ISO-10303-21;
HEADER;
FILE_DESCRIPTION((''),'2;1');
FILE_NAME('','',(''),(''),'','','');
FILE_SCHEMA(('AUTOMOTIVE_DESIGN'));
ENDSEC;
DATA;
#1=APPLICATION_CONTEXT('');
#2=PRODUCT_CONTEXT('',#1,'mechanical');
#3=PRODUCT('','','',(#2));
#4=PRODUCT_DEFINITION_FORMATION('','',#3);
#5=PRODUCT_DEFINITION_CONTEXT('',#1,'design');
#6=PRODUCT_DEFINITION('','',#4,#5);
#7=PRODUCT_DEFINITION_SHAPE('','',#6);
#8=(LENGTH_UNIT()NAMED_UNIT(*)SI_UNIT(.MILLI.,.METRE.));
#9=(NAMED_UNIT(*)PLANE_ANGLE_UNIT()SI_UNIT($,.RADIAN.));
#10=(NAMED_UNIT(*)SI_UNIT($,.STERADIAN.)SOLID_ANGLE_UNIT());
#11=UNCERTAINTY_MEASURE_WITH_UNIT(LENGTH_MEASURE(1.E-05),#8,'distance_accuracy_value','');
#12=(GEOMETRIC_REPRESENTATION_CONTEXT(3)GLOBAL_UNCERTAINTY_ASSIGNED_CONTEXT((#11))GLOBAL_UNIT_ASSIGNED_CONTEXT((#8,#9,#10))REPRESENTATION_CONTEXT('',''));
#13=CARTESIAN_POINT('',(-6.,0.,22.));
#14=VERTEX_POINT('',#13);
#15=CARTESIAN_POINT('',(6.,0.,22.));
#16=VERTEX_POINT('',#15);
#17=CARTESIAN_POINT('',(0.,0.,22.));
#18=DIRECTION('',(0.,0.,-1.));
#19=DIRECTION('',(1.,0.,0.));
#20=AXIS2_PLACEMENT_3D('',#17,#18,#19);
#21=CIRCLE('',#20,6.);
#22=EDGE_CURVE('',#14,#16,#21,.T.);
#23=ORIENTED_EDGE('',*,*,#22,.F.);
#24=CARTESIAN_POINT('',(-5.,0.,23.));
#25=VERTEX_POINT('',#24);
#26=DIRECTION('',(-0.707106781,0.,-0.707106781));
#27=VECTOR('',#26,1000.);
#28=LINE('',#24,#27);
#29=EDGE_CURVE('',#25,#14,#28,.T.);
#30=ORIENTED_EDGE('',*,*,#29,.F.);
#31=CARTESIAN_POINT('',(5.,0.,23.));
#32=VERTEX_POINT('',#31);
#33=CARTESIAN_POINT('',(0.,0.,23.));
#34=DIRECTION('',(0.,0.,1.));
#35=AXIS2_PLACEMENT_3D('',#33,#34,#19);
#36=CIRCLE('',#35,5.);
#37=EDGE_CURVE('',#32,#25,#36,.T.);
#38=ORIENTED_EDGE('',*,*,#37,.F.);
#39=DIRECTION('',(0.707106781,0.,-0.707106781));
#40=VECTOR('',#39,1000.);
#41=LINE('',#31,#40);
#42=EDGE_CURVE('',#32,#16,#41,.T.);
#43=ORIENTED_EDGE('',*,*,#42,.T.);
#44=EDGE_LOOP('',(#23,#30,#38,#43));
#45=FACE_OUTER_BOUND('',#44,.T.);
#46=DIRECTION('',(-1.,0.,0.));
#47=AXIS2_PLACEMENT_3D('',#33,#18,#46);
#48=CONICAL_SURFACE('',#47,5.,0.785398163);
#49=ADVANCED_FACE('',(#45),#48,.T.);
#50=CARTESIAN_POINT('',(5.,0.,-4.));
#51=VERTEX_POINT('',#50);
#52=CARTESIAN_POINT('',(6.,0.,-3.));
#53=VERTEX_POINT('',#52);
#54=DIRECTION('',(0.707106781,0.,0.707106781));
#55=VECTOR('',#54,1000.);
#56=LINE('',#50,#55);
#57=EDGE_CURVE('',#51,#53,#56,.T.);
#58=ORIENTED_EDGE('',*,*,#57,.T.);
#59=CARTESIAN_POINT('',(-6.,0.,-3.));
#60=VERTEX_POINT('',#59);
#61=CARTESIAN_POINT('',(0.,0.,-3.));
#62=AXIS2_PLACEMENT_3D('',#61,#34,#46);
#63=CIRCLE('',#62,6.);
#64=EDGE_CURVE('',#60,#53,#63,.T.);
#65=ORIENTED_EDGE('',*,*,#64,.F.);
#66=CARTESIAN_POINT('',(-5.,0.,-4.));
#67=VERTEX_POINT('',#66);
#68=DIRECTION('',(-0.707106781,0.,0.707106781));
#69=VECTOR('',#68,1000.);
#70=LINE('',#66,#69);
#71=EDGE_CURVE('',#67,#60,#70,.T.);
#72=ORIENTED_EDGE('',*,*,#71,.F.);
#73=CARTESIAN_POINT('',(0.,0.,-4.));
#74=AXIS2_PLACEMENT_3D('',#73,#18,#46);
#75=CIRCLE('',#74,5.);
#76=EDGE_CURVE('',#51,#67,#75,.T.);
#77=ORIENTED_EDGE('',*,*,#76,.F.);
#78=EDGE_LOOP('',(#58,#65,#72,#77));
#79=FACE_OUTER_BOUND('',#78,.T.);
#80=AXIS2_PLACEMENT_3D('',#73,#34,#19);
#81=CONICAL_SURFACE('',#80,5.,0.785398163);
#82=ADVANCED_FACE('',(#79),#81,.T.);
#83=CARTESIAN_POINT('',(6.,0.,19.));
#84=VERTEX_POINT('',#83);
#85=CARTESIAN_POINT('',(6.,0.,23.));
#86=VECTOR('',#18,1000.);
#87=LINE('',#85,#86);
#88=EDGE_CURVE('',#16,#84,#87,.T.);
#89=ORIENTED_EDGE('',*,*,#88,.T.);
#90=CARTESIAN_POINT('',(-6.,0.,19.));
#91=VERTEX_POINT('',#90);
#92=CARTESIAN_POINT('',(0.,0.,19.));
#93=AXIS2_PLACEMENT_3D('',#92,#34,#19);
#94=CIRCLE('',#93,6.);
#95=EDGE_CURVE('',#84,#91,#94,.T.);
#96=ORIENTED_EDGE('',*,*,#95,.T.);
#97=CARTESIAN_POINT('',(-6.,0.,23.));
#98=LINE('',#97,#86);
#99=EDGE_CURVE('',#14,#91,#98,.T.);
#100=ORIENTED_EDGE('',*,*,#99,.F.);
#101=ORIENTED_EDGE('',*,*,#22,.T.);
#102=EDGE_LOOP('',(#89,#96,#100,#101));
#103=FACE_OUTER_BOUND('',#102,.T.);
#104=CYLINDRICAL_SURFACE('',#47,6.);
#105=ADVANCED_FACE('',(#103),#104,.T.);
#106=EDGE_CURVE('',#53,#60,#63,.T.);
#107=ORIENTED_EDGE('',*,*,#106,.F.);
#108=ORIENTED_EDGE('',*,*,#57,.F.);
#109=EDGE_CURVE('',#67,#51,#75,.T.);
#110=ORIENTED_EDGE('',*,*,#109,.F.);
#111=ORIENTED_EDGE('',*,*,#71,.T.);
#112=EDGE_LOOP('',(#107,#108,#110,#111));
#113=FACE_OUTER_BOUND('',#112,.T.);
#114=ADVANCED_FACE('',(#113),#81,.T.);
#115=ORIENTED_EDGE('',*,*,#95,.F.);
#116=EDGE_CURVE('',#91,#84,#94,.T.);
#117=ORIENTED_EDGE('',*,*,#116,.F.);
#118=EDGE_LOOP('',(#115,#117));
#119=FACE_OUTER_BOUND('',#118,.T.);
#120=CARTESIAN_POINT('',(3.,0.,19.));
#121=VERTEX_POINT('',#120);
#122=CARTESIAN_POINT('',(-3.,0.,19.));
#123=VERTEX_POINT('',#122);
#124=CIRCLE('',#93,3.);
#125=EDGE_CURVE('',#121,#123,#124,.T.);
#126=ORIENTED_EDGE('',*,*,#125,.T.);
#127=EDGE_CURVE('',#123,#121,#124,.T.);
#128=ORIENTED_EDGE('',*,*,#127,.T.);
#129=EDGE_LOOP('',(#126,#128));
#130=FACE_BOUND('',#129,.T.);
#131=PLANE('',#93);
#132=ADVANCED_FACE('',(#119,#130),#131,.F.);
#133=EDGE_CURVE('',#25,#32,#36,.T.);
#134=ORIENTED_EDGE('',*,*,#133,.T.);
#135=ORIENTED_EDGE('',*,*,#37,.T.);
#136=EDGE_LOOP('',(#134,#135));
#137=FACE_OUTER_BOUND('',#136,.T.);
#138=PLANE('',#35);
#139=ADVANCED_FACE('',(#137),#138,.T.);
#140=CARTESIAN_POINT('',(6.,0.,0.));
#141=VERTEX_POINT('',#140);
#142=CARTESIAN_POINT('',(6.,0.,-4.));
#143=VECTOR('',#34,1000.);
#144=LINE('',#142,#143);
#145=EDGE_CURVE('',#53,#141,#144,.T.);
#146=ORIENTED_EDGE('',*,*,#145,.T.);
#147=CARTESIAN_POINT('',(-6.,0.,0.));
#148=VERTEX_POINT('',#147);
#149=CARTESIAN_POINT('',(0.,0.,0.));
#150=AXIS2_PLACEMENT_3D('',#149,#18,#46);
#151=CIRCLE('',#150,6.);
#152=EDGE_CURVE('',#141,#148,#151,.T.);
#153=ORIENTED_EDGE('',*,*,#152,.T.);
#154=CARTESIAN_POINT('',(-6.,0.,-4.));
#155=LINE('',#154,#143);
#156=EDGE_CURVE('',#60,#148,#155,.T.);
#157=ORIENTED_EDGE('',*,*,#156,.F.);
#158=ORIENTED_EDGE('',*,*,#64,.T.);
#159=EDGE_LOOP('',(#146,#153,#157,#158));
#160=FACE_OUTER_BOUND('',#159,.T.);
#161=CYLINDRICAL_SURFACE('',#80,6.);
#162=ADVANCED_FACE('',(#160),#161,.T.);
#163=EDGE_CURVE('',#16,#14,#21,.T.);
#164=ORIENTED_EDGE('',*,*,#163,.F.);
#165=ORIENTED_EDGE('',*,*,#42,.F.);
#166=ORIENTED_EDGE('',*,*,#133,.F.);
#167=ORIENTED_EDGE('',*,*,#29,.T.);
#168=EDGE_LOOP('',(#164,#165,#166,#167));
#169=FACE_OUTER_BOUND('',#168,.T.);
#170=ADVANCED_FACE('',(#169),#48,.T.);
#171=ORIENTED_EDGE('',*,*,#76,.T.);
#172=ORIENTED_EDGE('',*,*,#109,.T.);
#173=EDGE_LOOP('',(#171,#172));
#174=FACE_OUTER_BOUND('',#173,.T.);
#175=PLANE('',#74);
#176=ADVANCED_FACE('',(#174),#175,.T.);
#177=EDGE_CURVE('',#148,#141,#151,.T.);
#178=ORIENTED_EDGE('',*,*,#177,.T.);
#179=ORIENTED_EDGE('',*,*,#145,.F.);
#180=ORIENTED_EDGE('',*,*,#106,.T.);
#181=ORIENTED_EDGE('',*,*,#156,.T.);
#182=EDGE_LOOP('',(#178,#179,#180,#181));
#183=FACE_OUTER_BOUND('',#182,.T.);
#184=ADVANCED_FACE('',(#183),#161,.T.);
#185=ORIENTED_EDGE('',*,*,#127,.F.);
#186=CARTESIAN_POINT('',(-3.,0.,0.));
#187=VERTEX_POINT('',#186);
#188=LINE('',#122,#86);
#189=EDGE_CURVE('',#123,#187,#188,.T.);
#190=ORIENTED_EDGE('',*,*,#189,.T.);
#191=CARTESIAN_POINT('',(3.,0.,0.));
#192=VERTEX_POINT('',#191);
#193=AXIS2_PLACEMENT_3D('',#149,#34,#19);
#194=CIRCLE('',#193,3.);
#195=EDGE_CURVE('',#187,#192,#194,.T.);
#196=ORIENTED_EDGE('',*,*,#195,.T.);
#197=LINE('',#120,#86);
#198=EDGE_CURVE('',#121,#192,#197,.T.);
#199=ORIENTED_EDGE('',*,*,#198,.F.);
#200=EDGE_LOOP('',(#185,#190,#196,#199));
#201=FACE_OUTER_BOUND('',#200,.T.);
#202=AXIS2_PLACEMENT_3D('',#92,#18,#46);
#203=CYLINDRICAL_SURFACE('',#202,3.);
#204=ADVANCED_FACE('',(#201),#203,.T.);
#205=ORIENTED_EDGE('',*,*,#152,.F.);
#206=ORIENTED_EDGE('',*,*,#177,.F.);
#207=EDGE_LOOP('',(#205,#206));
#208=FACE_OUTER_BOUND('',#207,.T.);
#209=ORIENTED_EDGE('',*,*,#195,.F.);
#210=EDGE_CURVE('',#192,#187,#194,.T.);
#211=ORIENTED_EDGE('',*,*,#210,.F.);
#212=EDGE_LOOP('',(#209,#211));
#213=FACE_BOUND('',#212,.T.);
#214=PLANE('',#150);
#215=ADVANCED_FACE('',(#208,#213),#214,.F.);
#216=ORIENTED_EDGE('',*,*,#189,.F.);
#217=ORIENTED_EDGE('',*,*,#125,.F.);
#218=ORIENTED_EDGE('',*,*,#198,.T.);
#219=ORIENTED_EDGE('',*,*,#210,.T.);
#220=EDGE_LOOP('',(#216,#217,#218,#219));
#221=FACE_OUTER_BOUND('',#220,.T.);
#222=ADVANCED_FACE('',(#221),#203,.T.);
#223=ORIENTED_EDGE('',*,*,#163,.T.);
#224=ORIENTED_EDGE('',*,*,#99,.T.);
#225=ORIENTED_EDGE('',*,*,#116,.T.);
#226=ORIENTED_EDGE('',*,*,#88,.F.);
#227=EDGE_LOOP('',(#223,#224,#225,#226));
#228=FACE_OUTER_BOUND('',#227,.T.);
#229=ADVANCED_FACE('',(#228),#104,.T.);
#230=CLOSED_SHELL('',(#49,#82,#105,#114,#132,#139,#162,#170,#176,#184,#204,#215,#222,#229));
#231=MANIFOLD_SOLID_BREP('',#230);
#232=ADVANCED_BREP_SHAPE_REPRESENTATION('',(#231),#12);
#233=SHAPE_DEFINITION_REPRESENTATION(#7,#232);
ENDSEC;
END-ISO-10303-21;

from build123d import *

# Parameters (mm, degrees)
SKETCH_1_R      = 3
EXTRUDE_1_DEPTH = 19
SKETCH_2_R      = 6
EXTRUDE_2_DEPTH = 4
CHAMFER_1_SIZE  = 1
EXTRUDE_START   = 4
SKETCH_3_R      = 6
EXTRUDE_3_DEPTH = 4
CHAMFER_2_SIZE  = 1


with BuildPart() as part:
    # 草图1 → 凸台-拉伸1 (new body)
    with BuildSketch(Plane.XY):
        Circle(SKETCH_1_R)
    extrude(amount=EXTRUDE_1_DEPTH)

    # 草图2 → 凸台-拉伸2 (add)
    with BuildSketch(Plane.XY.offset(19)):
        Circle(SKETCH_2_R)
    extrude(amount=EXTRUDE_2_DEPTH)

    # 倒角1
    chamfer_1_edges = [part.edges().sort_by_distance(p)[0] for p in [
        (-6, 0, 23),
    ]]
    chamfer(chamfer_1_edges, length=CHAMFER_1_SIZE)

    # 草图3 → 凸台-拉伸3 (add)
    with BuildSketch(Plane(origin=(0, 0, 0), x_dir=(-1, 0, 0), z_dir=(0, 0, -1)).offset(EXTRUDE_START)):
        with Locations(Location((0, 0, 0), (0, 0, 180))):
            Circle(SKETCH_3_R)
    extrude(amount=-EXTRUDE_3_DEPTH)

    # 倒角2
    chamfer_2_edges = [part.edges().sort_by_distance(p)[0] for p in [
        (-6, 0, -4),
    ]]
    chamfer(chamfer_2_edges, length=CHAMFER_2_SIZE)


solid = part.part
